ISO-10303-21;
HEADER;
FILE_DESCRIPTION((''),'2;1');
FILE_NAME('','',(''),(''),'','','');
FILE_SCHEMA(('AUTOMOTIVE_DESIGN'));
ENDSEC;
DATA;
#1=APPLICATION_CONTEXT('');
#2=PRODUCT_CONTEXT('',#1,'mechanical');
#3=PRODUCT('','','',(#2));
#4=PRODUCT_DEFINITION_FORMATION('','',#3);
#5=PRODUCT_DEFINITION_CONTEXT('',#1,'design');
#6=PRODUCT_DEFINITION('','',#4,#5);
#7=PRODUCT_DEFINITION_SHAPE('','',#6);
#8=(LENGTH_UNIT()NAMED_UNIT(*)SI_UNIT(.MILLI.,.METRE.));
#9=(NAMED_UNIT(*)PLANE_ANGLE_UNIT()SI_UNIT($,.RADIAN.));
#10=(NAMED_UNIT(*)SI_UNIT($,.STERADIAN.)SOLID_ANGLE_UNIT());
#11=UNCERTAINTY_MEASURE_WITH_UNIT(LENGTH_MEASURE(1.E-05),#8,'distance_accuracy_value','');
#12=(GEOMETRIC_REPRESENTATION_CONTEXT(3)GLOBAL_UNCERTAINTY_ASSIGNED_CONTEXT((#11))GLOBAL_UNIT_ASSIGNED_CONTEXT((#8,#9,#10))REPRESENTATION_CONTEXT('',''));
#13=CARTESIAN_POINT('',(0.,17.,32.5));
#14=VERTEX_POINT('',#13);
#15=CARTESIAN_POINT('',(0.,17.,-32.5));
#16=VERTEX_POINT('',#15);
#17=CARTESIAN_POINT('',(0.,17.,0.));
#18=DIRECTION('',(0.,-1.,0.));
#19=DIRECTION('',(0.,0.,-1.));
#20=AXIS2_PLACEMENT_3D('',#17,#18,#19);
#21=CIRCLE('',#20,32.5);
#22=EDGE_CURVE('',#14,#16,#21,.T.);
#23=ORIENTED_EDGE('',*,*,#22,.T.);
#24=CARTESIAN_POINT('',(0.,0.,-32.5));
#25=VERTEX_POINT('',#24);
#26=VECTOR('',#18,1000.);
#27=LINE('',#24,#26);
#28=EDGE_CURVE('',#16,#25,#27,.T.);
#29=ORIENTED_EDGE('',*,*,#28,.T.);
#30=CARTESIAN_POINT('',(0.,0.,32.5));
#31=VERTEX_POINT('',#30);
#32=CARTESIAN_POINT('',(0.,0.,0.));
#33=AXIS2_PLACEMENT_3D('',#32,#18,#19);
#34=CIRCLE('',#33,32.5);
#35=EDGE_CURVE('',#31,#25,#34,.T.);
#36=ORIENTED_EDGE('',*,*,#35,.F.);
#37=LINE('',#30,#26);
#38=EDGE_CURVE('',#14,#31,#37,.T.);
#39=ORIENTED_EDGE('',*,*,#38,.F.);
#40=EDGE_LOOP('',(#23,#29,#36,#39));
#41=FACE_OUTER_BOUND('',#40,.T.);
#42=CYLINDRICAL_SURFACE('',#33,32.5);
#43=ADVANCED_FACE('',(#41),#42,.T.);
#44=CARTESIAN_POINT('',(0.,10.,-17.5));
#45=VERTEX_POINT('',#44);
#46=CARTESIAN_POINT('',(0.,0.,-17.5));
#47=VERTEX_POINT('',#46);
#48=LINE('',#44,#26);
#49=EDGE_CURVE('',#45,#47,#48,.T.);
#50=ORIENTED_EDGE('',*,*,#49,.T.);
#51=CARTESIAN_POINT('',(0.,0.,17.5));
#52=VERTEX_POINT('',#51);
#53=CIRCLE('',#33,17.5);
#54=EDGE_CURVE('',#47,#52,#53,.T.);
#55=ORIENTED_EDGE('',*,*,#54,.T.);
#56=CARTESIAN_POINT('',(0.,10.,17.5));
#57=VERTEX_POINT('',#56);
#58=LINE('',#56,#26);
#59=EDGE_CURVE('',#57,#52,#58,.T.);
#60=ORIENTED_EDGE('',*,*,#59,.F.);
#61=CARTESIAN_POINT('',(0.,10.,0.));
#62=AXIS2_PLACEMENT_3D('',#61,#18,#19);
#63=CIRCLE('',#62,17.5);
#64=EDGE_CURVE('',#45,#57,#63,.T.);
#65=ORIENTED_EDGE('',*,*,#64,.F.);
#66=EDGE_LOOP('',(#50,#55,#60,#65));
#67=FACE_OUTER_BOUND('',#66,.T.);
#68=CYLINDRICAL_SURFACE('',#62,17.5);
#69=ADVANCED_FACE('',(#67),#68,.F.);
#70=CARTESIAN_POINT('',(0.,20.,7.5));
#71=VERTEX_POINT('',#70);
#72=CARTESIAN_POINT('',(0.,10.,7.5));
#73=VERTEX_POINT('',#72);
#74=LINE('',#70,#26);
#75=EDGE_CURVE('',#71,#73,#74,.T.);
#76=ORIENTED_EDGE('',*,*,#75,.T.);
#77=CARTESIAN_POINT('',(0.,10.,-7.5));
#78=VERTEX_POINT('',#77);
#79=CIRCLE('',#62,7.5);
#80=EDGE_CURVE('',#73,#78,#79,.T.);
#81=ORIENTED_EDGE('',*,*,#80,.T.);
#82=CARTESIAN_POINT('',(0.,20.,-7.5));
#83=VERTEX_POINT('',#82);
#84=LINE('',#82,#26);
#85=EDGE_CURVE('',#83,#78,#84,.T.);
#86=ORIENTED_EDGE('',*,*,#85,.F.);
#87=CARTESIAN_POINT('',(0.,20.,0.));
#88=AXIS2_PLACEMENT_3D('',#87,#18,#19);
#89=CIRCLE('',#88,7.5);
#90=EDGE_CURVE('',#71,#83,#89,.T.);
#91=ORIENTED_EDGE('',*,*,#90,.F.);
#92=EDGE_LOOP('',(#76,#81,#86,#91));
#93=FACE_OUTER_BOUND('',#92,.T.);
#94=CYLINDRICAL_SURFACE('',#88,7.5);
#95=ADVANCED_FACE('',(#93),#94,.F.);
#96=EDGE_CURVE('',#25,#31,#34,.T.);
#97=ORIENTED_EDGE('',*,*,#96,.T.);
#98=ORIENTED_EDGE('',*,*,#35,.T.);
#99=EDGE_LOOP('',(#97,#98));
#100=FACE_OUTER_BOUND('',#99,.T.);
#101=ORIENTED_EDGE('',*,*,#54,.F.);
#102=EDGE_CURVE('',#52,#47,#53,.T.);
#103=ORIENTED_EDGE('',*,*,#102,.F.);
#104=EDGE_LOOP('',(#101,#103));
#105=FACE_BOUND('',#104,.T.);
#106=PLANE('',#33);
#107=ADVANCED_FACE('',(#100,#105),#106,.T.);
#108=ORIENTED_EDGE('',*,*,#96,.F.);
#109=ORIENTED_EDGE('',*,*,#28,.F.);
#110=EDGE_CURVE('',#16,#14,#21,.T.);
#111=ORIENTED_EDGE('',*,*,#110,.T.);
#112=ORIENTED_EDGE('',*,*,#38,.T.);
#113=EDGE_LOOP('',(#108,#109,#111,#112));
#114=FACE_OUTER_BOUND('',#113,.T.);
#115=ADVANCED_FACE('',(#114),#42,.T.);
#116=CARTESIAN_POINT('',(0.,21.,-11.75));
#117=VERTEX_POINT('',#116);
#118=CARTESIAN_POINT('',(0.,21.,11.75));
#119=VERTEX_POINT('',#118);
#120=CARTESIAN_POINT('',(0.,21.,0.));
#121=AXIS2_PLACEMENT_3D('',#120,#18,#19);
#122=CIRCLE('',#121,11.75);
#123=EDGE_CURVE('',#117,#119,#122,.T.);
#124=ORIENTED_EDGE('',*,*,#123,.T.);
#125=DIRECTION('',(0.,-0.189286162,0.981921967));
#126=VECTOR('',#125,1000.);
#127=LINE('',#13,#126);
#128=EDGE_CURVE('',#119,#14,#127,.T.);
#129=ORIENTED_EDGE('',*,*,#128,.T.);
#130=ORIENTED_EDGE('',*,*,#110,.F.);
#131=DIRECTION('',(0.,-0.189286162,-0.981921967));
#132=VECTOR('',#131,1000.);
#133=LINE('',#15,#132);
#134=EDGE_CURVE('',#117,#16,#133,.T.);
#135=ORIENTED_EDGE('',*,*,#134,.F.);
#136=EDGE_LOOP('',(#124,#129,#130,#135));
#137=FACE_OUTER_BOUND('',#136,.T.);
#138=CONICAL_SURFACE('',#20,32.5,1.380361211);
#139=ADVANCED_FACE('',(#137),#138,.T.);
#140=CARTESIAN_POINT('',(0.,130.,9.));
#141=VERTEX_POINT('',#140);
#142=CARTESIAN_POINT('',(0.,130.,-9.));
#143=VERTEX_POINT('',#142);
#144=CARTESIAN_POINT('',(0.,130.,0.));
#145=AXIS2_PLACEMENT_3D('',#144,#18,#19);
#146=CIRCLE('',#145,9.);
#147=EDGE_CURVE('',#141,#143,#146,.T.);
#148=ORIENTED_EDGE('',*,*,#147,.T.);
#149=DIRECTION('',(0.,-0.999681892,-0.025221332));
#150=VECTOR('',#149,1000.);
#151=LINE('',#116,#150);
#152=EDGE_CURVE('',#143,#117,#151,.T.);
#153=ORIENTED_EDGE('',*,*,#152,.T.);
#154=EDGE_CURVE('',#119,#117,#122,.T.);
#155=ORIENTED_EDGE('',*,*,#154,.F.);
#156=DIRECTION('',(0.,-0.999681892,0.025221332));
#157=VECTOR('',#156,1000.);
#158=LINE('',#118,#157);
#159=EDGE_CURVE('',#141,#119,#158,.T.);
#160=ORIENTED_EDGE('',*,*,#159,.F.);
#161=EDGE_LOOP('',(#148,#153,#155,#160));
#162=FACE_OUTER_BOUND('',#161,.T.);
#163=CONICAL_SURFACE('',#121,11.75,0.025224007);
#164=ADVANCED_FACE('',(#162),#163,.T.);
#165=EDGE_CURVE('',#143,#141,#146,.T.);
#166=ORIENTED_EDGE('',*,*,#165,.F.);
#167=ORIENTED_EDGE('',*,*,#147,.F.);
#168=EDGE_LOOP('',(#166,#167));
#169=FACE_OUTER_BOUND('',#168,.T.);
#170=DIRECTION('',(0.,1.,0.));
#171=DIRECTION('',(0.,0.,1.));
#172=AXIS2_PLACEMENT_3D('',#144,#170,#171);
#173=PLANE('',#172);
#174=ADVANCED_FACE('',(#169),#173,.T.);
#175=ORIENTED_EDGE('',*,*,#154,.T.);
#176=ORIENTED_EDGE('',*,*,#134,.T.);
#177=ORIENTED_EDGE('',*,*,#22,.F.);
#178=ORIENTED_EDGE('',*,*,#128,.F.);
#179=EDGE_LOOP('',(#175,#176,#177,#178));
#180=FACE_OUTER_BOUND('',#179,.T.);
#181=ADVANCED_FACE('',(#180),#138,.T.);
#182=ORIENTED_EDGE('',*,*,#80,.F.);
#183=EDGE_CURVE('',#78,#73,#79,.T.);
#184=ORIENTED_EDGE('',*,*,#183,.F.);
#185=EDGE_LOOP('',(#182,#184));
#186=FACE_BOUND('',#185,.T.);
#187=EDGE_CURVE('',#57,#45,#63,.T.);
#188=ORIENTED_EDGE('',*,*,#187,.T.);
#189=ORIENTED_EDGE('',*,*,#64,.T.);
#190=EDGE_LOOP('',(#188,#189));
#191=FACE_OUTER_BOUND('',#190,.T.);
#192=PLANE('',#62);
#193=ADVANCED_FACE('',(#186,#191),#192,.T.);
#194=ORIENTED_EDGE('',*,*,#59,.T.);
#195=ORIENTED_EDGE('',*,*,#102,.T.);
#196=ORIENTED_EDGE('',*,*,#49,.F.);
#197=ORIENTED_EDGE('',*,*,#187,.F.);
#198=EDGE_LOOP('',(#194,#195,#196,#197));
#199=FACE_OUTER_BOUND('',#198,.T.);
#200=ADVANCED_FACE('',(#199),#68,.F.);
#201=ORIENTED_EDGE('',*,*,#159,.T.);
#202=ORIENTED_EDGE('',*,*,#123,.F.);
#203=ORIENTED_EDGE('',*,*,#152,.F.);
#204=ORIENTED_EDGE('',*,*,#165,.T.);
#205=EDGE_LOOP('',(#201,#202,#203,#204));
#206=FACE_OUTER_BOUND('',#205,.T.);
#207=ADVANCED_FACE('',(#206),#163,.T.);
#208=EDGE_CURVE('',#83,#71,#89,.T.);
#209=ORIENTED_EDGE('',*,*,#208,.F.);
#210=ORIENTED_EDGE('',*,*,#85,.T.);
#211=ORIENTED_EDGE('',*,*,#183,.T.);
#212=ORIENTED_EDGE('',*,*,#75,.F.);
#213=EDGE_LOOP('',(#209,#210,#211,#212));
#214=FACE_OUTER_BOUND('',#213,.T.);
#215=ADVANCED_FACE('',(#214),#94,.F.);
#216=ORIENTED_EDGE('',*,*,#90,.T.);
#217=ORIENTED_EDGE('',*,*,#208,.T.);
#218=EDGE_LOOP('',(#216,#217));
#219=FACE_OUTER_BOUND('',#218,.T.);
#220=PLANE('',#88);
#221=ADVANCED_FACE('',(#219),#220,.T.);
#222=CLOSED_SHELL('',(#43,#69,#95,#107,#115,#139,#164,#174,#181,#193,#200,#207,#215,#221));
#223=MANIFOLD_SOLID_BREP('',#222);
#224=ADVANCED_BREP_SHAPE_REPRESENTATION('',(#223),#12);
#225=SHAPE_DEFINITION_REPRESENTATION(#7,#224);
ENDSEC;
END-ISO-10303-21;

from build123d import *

# Parameters (mm, degrees)
SKETCH_2_R          = 17.5
CUT_EXTRUDE_1_DEPTH = 10
SKETCH_3_R          = 7.5
CUT_EXTRUDE_2_DEPTH = 10


with BuildPart() as part:
    # 草图1 → 旋转1 (revolve)
    with BuildSketch(Plane(origin=(0, 0, 0), x_dir=(0, 0, -1), z_dir=(1, 0, 0))):
        Polygon((0, 0), (0, 130), (9, 130), (11.75, 21), (32.5, 17), (32.5, 0), align=None)
    revolve(axis=Axis((0, 0, 0), (0, 1, 0)))

    # 草图2 → 切除-拉伸1 (cut)
    with BuildSketch(Plane.XZ):
        with Locations(Location((0, 0, 0), (0, 0, 270))):
            Circle(SKETCH_2_R)
    extrude(amount=-CUT_EXTRUDE_1_DEPTH, mode=Mode.SUBTRACT)

    # 草图3 → 切除-拉伸2 (cut)
    with BuildSketch(Plane.XZ.offset(-10)):
        with Locations(Location((0, 0, 0), (0, 0, 270))):
            Circle(SKETCH_3_R)
    extrude(amount=-CUT_EXTRUDE_2_DEPTH, mode=Mode.SUBTRACT)


solid = part.part
